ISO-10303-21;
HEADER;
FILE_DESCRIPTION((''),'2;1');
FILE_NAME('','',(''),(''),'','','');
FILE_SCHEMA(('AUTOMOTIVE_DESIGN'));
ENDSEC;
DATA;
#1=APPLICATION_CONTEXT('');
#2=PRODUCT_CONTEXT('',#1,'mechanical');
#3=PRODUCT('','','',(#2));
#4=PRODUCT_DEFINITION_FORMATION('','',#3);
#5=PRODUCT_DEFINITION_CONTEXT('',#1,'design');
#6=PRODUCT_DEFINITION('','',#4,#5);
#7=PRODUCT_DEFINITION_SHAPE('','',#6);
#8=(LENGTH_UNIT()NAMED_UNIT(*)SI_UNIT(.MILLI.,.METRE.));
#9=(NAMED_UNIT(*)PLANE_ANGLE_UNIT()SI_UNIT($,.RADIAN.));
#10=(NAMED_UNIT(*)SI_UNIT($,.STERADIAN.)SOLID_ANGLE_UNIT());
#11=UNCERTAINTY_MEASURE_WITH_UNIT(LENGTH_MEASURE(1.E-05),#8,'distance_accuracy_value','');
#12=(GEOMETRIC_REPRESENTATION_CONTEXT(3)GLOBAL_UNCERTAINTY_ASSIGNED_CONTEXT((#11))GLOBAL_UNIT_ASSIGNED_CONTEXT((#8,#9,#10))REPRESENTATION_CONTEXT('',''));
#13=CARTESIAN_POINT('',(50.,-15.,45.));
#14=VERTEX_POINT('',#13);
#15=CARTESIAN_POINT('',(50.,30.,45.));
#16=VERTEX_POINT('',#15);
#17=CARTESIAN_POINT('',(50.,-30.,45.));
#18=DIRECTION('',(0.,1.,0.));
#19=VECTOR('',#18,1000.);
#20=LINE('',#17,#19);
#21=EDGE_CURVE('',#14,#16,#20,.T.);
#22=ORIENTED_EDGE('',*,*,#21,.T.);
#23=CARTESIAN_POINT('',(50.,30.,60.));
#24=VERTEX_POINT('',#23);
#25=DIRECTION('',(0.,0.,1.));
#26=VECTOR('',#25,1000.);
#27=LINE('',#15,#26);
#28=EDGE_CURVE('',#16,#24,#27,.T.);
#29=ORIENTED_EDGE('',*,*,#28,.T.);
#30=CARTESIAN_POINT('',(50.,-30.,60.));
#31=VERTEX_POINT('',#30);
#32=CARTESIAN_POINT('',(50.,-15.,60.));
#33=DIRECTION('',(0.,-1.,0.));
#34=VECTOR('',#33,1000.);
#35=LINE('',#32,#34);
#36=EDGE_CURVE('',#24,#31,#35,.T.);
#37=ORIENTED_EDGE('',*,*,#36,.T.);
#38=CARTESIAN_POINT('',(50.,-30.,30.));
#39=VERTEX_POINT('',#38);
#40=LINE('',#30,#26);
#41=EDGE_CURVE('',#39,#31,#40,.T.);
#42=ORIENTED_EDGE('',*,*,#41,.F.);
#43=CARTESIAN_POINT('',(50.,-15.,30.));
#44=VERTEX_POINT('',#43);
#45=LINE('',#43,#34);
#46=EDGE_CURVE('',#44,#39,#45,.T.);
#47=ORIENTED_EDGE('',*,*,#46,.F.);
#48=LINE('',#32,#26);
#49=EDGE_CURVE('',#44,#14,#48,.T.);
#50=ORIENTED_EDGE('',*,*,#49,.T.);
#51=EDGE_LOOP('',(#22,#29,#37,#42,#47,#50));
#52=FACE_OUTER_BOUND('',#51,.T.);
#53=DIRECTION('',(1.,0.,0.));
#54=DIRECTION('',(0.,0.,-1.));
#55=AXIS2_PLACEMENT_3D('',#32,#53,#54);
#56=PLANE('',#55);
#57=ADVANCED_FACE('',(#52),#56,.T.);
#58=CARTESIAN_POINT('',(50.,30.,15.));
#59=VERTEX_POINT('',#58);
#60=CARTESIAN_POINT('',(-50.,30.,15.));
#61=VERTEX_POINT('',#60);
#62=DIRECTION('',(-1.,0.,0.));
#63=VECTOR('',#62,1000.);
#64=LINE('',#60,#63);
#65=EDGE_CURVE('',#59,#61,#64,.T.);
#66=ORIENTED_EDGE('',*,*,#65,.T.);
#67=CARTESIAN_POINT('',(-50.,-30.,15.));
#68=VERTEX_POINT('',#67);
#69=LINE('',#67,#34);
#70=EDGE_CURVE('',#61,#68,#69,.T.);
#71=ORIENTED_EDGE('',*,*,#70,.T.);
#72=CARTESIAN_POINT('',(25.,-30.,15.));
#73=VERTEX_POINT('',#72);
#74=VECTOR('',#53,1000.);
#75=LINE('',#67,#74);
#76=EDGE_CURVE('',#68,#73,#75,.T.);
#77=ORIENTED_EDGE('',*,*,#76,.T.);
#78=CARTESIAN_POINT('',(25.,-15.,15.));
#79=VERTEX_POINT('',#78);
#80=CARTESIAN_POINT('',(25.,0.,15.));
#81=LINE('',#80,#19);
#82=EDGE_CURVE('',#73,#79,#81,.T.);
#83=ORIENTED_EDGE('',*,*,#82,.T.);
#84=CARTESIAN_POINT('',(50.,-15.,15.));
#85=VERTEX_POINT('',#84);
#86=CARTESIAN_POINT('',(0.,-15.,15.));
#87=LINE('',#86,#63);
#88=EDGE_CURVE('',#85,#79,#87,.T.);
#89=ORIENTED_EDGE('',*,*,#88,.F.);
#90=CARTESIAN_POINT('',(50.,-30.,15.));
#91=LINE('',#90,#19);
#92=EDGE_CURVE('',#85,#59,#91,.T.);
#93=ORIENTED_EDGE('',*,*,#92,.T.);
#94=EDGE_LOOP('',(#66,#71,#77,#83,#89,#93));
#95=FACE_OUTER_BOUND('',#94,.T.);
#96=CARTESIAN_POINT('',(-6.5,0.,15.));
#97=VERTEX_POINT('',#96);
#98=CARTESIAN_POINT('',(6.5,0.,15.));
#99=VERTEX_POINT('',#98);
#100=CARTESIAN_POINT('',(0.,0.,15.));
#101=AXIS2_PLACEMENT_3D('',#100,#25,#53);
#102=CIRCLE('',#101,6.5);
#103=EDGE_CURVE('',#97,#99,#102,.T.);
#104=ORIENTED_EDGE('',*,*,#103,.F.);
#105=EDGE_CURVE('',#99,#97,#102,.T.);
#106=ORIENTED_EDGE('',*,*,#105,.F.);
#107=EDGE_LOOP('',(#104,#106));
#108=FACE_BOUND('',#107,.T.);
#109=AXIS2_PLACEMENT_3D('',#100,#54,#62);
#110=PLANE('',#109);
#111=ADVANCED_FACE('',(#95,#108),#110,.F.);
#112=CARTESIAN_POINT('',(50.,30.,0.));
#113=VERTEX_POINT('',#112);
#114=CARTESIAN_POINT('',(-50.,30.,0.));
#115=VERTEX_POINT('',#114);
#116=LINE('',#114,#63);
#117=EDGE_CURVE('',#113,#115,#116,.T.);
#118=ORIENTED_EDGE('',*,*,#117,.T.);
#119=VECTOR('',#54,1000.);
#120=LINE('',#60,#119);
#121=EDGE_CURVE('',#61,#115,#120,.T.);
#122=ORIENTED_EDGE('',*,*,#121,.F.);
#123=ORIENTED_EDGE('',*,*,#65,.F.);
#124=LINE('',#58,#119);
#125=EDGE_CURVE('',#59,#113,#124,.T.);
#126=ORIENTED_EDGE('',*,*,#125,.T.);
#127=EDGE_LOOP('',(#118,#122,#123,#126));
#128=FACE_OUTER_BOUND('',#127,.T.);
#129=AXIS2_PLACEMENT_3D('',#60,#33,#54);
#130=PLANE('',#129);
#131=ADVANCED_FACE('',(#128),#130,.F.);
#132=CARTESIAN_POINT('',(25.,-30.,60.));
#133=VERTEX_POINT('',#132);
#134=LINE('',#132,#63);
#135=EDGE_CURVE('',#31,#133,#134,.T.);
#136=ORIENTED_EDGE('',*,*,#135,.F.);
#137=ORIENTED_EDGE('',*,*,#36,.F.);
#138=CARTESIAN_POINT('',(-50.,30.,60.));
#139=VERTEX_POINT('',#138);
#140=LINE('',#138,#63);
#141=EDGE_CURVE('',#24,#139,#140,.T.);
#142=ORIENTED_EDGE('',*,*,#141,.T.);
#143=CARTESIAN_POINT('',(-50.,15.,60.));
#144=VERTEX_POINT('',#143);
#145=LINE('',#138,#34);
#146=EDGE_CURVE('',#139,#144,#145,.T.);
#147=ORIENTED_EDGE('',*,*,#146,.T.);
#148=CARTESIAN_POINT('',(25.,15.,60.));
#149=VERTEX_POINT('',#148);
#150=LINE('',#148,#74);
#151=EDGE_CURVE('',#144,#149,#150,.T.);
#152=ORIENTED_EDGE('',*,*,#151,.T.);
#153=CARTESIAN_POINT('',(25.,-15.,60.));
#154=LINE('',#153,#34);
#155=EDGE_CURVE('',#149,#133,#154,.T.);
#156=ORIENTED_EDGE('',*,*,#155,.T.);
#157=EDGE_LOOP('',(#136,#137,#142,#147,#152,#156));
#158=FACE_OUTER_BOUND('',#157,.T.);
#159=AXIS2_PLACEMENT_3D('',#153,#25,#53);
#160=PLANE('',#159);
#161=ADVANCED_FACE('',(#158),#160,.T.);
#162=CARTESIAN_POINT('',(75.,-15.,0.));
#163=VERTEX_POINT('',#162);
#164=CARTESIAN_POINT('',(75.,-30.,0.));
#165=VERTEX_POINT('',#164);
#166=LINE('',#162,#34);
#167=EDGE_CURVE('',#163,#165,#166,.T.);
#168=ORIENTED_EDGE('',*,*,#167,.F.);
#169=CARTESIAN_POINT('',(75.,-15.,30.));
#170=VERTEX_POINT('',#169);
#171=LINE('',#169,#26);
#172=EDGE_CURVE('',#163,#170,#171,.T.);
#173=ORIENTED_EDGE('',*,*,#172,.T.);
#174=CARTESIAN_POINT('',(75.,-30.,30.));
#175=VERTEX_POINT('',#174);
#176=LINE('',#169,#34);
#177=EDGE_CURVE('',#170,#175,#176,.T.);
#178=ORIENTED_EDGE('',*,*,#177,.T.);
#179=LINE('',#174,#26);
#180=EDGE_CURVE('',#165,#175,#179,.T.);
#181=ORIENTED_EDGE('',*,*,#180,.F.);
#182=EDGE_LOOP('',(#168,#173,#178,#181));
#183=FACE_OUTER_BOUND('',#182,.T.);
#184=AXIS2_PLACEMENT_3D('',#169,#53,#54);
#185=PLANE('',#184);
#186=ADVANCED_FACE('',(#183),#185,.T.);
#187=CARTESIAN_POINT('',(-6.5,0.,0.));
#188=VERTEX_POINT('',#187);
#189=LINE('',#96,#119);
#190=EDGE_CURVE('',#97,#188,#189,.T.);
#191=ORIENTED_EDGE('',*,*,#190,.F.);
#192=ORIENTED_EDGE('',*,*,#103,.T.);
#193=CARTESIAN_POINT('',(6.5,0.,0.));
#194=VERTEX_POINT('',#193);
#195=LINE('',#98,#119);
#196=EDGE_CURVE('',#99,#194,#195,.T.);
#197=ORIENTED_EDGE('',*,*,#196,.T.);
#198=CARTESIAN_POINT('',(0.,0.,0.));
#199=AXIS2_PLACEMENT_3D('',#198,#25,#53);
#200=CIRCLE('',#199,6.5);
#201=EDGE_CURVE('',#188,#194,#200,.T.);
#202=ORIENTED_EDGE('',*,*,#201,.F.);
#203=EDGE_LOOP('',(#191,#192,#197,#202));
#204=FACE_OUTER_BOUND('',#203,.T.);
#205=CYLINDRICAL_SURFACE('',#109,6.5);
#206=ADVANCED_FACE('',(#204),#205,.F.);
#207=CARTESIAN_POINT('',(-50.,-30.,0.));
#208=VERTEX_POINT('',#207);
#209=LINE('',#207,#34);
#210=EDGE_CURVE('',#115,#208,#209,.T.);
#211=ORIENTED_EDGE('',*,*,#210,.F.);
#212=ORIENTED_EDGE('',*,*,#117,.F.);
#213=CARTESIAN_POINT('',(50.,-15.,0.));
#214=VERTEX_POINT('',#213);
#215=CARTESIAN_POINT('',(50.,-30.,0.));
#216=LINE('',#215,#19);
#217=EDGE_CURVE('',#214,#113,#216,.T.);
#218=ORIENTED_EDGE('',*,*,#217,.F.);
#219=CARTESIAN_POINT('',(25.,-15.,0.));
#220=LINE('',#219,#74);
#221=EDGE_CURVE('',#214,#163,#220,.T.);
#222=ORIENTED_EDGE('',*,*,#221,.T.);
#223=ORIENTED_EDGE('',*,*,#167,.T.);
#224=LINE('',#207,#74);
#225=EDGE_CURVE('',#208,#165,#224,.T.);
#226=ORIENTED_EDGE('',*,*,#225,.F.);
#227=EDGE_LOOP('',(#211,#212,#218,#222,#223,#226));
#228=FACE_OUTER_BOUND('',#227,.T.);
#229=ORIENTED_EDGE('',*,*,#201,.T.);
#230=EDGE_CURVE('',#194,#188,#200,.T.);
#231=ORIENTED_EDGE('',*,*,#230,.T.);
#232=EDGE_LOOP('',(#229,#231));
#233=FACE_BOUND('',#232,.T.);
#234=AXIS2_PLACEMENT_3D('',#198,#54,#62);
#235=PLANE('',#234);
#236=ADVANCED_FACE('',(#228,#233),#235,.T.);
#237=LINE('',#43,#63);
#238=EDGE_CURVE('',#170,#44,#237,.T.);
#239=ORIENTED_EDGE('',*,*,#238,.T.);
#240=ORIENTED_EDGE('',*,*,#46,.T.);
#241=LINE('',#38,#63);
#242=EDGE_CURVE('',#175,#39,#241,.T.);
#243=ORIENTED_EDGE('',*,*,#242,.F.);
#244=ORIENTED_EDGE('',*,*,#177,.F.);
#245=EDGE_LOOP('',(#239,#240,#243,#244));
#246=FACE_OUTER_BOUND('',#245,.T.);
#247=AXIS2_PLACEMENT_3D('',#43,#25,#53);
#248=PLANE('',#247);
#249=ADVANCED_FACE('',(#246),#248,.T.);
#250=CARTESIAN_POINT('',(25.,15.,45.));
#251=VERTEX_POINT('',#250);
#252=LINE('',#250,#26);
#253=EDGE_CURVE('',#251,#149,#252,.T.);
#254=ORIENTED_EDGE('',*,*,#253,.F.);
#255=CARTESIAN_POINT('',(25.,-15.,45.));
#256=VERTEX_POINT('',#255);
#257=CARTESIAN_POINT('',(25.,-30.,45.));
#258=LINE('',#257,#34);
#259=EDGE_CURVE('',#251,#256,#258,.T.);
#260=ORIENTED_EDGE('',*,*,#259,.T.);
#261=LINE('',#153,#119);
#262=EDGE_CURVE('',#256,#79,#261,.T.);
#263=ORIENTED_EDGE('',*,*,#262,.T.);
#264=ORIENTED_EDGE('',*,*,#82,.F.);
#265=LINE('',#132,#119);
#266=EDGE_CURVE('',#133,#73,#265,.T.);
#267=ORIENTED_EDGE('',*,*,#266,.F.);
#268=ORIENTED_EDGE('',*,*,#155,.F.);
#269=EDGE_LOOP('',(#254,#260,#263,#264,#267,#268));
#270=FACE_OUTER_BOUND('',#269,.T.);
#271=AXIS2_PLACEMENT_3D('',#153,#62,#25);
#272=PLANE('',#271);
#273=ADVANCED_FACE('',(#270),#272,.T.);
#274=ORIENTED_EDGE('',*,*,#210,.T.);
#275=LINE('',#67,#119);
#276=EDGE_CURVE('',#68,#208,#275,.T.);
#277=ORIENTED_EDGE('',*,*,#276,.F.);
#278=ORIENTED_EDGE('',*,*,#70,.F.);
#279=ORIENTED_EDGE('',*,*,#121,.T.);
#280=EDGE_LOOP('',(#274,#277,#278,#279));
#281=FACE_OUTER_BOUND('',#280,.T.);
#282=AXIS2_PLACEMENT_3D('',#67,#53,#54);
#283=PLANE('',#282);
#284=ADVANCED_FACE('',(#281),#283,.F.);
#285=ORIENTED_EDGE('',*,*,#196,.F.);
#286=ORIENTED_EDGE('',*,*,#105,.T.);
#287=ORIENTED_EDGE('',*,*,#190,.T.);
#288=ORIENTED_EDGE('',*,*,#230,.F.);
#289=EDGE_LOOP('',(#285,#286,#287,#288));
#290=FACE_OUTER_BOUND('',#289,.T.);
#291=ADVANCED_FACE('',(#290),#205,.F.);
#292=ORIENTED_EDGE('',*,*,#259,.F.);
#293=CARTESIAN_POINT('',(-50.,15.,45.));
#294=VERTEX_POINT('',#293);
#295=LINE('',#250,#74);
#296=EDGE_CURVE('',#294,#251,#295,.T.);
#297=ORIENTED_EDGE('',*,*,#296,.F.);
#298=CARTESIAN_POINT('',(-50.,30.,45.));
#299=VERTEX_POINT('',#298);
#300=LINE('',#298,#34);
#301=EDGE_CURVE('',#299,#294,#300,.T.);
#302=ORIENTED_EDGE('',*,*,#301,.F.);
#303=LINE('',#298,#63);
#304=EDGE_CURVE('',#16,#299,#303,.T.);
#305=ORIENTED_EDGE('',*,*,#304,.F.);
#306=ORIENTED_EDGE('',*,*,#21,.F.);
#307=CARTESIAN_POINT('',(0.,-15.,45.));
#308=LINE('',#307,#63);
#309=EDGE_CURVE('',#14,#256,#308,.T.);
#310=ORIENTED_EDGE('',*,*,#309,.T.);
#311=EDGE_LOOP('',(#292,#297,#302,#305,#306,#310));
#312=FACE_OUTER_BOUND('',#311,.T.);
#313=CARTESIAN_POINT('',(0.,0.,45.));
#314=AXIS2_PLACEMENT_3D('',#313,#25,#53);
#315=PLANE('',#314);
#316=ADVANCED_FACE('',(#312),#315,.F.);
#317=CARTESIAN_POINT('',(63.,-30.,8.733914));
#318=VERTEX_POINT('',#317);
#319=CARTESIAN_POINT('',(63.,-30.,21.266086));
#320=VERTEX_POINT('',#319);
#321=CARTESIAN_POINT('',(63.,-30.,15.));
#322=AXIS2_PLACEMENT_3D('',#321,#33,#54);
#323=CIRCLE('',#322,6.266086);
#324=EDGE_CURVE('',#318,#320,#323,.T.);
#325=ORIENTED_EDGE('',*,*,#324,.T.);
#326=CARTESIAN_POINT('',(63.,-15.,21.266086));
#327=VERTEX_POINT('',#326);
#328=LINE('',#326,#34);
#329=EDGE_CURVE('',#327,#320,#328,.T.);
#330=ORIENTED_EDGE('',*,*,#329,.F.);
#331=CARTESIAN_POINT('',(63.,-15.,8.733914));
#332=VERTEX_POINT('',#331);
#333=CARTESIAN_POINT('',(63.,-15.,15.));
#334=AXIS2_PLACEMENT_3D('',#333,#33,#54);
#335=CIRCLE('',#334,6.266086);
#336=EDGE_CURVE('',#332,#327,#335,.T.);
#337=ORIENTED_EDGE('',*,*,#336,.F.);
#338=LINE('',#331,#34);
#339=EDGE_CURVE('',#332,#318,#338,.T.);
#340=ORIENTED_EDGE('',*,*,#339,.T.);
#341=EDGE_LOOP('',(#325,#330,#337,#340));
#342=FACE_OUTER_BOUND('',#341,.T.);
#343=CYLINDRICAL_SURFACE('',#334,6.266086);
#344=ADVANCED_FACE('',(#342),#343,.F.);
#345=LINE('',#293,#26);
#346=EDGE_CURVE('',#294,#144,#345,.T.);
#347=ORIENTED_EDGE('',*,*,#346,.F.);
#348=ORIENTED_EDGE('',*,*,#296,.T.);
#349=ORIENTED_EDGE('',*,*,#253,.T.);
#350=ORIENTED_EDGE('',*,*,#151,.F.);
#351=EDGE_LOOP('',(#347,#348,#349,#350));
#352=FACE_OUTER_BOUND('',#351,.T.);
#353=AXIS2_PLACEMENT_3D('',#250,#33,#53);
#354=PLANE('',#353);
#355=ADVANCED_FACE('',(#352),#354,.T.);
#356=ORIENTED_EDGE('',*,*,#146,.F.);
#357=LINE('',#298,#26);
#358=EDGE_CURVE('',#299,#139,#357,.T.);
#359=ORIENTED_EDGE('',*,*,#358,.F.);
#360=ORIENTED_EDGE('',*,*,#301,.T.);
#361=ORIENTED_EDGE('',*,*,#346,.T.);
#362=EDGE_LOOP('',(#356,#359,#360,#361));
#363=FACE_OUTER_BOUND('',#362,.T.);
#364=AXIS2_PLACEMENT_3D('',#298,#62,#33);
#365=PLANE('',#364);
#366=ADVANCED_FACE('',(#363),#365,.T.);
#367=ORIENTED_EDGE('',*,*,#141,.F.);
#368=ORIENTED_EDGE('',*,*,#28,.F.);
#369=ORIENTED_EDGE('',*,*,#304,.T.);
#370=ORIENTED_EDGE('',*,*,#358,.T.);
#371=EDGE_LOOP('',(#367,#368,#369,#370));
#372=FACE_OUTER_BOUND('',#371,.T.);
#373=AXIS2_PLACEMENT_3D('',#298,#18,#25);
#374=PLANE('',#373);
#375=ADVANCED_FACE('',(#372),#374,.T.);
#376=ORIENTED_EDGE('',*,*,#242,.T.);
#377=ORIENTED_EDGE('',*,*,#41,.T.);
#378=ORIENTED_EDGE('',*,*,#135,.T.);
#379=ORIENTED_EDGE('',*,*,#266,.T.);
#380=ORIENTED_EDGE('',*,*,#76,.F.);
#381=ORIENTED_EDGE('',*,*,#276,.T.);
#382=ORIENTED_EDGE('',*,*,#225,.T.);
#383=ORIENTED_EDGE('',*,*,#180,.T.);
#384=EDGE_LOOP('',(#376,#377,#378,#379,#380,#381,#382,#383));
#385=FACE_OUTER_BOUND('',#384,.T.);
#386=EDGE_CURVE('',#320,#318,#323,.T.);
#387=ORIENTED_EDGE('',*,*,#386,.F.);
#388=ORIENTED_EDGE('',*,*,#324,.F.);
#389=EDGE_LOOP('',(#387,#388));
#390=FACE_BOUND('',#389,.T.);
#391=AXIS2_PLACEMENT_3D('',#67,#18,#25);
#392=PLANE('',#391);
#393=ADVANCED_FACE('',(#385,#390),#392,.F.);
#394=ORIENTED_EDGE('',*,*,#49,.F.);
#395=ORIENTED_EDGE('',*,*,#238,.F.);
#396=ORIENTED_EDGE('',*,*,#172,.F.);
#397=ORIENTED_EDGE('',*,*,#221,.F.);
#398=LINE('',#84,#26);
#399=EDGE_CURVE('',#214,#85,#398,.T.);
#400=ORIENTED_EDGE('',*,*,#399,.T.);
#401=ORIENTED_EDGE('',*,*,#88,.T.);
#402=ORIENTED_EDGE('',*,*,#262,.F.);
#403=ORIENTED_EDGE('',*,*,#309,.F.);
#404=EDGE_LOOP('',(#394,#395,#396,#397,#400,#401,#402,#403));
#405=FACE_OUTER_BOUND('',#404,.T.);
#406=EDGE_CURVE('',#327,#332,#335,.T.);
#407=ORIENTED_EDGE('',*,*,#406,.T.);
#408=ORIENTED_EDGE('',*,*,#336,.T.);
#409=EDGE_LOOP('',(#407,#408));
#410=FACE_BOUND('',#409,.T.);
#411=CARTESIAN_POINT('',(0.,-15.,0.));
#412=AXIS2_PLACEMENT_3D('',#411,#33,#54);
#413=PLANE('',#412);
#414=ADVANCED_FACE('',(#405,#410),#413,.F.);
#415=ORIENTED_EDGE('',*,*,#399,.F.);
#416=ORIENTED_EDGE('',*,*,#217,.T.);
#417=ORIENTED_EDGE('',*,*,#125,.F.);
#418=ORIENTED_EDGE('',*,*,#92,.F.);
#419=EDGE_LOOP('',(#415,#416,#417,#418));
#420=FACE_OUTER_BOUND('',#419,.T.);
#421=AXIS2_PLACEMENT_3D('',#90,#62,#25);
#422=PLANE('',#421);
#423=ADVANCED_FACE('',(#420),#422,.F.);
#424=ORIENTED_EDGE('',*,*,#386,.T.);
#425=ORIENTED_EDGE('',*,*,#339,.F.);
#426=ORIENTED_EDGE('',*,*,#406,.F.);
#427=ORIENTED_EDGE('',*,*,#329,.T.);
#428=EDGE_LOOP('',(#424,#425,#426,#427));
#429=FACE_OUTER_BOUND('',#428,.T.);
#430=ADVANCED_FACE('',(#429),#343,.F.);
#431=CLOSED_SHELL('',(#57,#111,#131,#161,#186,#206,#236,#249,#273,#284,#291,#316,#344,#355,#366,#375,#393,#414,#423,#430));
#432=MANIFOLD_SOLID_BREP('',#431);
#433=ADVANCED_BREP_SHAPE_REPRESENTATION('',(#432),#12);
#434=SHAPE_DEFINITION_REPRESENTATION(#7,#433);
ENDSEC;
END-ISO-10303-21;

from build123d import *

# Parameters (mm, degrees)
CHANNEL_PROFILE_SKETCH_W = 100
CHANNEL_PROFILE_SKETCH_H = 60
CHANNEL_PROFILE_SKETCH_R = 6.5
CHANNEL_BODY_DEPTH       = 15
LUG_1_PROFILE_SKETCH_R   = 6.266086447
PIERCED_LUG_1_DEPTH      = 15
PIERCED_LUG_2_DEPTH      = 15


with BuildPart() as part:
    # Channel Profile Sketch → Channel Body (new body)
    with BuildSketch(Plane.XY):
        Rectangle(CHANNEL_PROFILE_SKETCH_W, CHANNEL_PROFILE_SKETCH_H)
        Circle(CHANNEL_PROFILE_SKETCH_R, mode=Mode.SUBTRACT)
    extrude(amount=CHANNEL_BODY_DEPTH)

    # Lug 1 Profile Sketch → Pierced Lug 1 (add)
    with BuildSketch(Plane.XZ.offset(30)):
        Polygon((25, 0), (75, 0), (75, 30), (50, 30), (50, 60), (25, 60), align=None)
        with Locations(Location((63, 15, 0), (0, 0, 270))):
            Circle(LUG_1_PROFILE_SKETCH_R, mode=Mode.SUBTRACT)
    extrude(amount=-PIERCED_LUG_1_DEPTH)

    # Lug 2 Profile Sketch → Pierced Lug 2 (add)
    with BuildSketch(Plane.XY.offset(60)):
        Polygon((25, -30), (50, -30), (50, 30), (-50, 30), (-50, 15), (25, 15), align=None)
    extrude(amount=-PIERCED_LUG_2_DEPTH)


solid = part.part
